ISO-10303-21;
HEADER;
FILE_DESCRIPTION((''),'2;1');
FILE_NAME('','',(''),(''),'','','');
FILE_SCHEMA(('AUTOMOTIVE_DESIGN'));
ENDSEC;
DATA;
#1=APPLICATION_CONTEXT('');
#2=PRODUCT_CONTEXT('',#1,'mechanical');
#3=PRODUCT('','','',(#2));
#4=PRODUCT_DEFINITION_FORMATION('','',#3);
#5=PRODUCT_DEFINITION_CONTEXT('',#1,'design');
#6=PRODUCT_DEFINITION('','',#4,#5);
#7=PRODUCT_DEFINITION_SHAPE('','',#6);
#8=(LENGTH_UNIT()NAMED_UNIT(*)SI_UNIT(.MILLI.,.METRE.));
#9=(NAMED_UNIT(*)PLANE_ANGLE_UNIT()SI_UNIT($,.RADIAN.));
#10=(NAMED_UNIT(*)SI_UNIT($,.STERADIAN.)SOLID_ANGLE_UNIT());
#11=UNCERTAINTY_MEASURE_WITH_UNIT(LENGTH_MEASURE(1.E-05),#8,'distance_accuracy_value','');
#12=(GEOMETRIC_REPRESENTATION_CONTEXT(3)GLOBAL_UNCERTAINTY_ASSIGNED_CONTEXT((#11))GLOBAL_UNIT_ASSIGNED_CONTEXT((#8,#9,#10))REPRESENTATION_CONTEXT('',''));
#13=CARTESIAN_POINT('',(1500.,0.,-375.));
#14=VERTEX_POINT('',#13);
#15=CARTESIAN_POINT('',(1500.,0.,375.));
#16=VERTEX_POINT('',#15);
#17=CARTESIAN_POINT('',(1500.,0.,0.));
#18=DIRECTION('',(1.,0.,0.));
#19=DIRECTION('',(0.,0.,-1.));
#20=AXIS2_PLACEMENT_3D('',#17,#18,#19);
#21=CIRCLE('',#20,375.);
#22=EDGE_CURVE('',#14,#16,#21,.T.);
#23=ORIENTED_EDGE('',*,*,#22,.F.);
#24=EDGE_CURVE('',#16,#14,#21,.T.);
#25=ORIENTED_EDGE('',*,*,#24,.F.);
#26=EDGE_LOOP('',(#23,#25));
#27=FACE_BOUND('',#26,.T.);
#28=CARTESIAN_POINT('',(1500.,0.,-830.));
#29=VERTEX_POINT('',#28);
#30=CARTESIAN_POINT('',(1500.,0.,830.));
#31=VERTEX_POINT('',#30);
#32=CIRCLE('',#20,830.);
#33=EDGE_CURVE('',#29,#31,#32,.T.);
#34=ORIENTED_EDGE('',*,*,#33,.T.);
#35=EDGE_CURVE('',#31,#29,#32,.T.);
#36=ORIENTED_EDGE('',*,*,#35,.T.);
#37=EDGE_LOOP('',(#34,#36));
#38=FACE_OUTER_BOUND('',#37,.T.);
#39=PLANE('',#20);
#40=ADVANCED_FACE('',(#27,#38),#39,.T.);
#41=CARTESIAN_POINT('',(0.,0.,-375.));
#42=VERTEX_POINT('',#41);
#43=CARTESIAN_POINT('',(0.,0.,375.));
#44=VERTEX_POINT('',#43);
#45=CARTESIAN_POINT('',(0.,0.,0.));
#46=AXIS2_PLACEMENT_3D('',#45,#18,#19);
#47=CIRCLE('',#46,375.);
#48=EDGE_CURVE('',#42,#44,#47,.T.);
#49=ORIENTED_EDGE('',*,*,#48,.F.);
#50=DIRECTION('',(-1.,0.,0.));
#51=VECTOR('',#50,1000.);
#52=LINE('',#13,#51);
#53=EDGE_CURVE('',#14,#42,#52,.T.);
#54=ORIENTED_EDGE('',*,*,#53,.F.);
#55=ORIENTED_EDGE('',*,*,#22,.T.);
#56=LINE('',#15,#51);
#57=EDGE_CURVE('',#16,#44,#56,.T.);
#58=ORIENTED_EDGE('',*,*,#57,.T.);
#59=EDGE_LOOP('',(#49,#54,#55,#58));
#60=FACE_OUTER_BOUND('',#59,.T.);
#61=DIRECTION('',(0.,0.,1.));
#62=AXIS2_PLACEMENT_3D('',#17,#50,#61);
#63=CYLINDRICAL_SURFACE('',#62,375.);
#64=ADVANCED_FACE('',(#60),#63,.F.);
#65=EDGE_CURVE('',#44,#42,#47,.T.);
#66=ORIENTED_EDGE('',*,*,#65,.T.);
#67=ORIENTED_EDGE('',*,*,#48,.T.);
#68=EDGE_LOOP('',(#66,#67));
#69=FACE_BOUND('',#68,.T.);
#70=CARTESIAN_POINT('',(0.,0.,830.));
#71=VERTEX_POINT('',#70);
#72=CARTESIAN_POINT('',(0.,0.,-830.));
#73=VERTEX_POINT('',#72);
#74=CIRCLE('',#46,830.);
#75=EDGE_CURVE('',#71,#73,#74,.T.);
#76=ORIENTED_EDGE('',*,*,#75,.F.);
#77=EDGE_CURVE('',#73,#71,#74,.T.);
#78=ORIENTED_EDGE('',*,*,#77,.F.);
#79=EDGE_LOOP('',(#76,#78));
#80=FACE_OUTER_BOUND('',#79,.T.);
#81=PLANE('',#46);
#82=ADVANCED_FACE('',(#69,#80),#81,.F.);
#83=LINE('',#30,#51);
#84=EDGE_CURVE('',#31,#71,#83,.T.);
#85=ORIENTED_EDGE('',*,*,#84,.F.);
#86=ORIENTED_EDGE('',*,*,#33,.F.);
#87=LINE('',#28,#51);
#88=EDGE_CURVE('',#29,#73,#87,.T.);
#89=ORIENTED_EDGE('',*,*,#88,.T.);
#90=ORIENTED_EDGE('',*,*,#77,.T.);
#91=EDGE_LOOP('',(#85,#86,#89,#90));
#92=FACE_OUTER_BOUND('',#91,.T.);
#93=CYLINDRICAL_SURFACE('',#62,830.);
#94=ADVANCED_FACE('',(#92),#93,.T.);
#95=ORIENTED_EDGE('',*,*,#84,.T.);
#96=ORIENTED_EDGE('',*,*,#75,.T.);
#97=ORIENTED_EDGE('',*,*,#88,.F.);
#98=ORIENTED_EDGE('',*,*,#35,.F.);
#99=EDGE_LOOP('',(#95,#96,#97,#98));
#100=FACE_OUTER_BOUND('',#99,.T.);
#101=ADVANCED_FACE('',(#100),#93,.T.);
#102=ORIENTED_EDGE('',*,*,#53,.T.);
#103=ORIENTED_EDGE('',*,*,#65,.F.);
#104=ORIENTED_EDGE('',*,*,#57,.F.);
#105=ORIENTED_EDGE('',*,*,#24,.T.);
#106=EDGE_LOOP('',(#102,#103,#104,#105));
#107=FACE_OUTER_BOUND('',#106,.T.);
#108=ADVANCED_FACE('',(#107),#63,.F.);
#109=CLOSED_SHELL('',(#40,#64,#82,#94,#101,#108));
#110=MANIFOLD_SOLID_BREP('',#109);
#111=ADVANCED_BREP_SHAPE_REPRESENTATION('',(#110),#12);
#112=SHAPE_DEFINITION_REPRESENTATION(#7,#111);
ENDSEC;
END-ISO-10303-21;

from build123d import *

# Parameters (mm, degrees)
SKETCH1_R           = 830
SKETCH1_R_2         = 375
BOSS_EXTRUDE1_DEPTH = 1500


with BuildPart() as part:
    # Sketch1 → Boss-Extrude1 (new body)
    with BuildSketch(Plane(origin=(0, 0, 0), x_dir=(0, 0, -1), z_dir=(1, 0, 0))):
        Circle(SKETCH1_R)
        Circle(SKETCH1_R_2, mode=Mode.SUBTRACT)
    extrude(amount=BOSS_EXTRUDE1_DEPTH)


solid = part.part
